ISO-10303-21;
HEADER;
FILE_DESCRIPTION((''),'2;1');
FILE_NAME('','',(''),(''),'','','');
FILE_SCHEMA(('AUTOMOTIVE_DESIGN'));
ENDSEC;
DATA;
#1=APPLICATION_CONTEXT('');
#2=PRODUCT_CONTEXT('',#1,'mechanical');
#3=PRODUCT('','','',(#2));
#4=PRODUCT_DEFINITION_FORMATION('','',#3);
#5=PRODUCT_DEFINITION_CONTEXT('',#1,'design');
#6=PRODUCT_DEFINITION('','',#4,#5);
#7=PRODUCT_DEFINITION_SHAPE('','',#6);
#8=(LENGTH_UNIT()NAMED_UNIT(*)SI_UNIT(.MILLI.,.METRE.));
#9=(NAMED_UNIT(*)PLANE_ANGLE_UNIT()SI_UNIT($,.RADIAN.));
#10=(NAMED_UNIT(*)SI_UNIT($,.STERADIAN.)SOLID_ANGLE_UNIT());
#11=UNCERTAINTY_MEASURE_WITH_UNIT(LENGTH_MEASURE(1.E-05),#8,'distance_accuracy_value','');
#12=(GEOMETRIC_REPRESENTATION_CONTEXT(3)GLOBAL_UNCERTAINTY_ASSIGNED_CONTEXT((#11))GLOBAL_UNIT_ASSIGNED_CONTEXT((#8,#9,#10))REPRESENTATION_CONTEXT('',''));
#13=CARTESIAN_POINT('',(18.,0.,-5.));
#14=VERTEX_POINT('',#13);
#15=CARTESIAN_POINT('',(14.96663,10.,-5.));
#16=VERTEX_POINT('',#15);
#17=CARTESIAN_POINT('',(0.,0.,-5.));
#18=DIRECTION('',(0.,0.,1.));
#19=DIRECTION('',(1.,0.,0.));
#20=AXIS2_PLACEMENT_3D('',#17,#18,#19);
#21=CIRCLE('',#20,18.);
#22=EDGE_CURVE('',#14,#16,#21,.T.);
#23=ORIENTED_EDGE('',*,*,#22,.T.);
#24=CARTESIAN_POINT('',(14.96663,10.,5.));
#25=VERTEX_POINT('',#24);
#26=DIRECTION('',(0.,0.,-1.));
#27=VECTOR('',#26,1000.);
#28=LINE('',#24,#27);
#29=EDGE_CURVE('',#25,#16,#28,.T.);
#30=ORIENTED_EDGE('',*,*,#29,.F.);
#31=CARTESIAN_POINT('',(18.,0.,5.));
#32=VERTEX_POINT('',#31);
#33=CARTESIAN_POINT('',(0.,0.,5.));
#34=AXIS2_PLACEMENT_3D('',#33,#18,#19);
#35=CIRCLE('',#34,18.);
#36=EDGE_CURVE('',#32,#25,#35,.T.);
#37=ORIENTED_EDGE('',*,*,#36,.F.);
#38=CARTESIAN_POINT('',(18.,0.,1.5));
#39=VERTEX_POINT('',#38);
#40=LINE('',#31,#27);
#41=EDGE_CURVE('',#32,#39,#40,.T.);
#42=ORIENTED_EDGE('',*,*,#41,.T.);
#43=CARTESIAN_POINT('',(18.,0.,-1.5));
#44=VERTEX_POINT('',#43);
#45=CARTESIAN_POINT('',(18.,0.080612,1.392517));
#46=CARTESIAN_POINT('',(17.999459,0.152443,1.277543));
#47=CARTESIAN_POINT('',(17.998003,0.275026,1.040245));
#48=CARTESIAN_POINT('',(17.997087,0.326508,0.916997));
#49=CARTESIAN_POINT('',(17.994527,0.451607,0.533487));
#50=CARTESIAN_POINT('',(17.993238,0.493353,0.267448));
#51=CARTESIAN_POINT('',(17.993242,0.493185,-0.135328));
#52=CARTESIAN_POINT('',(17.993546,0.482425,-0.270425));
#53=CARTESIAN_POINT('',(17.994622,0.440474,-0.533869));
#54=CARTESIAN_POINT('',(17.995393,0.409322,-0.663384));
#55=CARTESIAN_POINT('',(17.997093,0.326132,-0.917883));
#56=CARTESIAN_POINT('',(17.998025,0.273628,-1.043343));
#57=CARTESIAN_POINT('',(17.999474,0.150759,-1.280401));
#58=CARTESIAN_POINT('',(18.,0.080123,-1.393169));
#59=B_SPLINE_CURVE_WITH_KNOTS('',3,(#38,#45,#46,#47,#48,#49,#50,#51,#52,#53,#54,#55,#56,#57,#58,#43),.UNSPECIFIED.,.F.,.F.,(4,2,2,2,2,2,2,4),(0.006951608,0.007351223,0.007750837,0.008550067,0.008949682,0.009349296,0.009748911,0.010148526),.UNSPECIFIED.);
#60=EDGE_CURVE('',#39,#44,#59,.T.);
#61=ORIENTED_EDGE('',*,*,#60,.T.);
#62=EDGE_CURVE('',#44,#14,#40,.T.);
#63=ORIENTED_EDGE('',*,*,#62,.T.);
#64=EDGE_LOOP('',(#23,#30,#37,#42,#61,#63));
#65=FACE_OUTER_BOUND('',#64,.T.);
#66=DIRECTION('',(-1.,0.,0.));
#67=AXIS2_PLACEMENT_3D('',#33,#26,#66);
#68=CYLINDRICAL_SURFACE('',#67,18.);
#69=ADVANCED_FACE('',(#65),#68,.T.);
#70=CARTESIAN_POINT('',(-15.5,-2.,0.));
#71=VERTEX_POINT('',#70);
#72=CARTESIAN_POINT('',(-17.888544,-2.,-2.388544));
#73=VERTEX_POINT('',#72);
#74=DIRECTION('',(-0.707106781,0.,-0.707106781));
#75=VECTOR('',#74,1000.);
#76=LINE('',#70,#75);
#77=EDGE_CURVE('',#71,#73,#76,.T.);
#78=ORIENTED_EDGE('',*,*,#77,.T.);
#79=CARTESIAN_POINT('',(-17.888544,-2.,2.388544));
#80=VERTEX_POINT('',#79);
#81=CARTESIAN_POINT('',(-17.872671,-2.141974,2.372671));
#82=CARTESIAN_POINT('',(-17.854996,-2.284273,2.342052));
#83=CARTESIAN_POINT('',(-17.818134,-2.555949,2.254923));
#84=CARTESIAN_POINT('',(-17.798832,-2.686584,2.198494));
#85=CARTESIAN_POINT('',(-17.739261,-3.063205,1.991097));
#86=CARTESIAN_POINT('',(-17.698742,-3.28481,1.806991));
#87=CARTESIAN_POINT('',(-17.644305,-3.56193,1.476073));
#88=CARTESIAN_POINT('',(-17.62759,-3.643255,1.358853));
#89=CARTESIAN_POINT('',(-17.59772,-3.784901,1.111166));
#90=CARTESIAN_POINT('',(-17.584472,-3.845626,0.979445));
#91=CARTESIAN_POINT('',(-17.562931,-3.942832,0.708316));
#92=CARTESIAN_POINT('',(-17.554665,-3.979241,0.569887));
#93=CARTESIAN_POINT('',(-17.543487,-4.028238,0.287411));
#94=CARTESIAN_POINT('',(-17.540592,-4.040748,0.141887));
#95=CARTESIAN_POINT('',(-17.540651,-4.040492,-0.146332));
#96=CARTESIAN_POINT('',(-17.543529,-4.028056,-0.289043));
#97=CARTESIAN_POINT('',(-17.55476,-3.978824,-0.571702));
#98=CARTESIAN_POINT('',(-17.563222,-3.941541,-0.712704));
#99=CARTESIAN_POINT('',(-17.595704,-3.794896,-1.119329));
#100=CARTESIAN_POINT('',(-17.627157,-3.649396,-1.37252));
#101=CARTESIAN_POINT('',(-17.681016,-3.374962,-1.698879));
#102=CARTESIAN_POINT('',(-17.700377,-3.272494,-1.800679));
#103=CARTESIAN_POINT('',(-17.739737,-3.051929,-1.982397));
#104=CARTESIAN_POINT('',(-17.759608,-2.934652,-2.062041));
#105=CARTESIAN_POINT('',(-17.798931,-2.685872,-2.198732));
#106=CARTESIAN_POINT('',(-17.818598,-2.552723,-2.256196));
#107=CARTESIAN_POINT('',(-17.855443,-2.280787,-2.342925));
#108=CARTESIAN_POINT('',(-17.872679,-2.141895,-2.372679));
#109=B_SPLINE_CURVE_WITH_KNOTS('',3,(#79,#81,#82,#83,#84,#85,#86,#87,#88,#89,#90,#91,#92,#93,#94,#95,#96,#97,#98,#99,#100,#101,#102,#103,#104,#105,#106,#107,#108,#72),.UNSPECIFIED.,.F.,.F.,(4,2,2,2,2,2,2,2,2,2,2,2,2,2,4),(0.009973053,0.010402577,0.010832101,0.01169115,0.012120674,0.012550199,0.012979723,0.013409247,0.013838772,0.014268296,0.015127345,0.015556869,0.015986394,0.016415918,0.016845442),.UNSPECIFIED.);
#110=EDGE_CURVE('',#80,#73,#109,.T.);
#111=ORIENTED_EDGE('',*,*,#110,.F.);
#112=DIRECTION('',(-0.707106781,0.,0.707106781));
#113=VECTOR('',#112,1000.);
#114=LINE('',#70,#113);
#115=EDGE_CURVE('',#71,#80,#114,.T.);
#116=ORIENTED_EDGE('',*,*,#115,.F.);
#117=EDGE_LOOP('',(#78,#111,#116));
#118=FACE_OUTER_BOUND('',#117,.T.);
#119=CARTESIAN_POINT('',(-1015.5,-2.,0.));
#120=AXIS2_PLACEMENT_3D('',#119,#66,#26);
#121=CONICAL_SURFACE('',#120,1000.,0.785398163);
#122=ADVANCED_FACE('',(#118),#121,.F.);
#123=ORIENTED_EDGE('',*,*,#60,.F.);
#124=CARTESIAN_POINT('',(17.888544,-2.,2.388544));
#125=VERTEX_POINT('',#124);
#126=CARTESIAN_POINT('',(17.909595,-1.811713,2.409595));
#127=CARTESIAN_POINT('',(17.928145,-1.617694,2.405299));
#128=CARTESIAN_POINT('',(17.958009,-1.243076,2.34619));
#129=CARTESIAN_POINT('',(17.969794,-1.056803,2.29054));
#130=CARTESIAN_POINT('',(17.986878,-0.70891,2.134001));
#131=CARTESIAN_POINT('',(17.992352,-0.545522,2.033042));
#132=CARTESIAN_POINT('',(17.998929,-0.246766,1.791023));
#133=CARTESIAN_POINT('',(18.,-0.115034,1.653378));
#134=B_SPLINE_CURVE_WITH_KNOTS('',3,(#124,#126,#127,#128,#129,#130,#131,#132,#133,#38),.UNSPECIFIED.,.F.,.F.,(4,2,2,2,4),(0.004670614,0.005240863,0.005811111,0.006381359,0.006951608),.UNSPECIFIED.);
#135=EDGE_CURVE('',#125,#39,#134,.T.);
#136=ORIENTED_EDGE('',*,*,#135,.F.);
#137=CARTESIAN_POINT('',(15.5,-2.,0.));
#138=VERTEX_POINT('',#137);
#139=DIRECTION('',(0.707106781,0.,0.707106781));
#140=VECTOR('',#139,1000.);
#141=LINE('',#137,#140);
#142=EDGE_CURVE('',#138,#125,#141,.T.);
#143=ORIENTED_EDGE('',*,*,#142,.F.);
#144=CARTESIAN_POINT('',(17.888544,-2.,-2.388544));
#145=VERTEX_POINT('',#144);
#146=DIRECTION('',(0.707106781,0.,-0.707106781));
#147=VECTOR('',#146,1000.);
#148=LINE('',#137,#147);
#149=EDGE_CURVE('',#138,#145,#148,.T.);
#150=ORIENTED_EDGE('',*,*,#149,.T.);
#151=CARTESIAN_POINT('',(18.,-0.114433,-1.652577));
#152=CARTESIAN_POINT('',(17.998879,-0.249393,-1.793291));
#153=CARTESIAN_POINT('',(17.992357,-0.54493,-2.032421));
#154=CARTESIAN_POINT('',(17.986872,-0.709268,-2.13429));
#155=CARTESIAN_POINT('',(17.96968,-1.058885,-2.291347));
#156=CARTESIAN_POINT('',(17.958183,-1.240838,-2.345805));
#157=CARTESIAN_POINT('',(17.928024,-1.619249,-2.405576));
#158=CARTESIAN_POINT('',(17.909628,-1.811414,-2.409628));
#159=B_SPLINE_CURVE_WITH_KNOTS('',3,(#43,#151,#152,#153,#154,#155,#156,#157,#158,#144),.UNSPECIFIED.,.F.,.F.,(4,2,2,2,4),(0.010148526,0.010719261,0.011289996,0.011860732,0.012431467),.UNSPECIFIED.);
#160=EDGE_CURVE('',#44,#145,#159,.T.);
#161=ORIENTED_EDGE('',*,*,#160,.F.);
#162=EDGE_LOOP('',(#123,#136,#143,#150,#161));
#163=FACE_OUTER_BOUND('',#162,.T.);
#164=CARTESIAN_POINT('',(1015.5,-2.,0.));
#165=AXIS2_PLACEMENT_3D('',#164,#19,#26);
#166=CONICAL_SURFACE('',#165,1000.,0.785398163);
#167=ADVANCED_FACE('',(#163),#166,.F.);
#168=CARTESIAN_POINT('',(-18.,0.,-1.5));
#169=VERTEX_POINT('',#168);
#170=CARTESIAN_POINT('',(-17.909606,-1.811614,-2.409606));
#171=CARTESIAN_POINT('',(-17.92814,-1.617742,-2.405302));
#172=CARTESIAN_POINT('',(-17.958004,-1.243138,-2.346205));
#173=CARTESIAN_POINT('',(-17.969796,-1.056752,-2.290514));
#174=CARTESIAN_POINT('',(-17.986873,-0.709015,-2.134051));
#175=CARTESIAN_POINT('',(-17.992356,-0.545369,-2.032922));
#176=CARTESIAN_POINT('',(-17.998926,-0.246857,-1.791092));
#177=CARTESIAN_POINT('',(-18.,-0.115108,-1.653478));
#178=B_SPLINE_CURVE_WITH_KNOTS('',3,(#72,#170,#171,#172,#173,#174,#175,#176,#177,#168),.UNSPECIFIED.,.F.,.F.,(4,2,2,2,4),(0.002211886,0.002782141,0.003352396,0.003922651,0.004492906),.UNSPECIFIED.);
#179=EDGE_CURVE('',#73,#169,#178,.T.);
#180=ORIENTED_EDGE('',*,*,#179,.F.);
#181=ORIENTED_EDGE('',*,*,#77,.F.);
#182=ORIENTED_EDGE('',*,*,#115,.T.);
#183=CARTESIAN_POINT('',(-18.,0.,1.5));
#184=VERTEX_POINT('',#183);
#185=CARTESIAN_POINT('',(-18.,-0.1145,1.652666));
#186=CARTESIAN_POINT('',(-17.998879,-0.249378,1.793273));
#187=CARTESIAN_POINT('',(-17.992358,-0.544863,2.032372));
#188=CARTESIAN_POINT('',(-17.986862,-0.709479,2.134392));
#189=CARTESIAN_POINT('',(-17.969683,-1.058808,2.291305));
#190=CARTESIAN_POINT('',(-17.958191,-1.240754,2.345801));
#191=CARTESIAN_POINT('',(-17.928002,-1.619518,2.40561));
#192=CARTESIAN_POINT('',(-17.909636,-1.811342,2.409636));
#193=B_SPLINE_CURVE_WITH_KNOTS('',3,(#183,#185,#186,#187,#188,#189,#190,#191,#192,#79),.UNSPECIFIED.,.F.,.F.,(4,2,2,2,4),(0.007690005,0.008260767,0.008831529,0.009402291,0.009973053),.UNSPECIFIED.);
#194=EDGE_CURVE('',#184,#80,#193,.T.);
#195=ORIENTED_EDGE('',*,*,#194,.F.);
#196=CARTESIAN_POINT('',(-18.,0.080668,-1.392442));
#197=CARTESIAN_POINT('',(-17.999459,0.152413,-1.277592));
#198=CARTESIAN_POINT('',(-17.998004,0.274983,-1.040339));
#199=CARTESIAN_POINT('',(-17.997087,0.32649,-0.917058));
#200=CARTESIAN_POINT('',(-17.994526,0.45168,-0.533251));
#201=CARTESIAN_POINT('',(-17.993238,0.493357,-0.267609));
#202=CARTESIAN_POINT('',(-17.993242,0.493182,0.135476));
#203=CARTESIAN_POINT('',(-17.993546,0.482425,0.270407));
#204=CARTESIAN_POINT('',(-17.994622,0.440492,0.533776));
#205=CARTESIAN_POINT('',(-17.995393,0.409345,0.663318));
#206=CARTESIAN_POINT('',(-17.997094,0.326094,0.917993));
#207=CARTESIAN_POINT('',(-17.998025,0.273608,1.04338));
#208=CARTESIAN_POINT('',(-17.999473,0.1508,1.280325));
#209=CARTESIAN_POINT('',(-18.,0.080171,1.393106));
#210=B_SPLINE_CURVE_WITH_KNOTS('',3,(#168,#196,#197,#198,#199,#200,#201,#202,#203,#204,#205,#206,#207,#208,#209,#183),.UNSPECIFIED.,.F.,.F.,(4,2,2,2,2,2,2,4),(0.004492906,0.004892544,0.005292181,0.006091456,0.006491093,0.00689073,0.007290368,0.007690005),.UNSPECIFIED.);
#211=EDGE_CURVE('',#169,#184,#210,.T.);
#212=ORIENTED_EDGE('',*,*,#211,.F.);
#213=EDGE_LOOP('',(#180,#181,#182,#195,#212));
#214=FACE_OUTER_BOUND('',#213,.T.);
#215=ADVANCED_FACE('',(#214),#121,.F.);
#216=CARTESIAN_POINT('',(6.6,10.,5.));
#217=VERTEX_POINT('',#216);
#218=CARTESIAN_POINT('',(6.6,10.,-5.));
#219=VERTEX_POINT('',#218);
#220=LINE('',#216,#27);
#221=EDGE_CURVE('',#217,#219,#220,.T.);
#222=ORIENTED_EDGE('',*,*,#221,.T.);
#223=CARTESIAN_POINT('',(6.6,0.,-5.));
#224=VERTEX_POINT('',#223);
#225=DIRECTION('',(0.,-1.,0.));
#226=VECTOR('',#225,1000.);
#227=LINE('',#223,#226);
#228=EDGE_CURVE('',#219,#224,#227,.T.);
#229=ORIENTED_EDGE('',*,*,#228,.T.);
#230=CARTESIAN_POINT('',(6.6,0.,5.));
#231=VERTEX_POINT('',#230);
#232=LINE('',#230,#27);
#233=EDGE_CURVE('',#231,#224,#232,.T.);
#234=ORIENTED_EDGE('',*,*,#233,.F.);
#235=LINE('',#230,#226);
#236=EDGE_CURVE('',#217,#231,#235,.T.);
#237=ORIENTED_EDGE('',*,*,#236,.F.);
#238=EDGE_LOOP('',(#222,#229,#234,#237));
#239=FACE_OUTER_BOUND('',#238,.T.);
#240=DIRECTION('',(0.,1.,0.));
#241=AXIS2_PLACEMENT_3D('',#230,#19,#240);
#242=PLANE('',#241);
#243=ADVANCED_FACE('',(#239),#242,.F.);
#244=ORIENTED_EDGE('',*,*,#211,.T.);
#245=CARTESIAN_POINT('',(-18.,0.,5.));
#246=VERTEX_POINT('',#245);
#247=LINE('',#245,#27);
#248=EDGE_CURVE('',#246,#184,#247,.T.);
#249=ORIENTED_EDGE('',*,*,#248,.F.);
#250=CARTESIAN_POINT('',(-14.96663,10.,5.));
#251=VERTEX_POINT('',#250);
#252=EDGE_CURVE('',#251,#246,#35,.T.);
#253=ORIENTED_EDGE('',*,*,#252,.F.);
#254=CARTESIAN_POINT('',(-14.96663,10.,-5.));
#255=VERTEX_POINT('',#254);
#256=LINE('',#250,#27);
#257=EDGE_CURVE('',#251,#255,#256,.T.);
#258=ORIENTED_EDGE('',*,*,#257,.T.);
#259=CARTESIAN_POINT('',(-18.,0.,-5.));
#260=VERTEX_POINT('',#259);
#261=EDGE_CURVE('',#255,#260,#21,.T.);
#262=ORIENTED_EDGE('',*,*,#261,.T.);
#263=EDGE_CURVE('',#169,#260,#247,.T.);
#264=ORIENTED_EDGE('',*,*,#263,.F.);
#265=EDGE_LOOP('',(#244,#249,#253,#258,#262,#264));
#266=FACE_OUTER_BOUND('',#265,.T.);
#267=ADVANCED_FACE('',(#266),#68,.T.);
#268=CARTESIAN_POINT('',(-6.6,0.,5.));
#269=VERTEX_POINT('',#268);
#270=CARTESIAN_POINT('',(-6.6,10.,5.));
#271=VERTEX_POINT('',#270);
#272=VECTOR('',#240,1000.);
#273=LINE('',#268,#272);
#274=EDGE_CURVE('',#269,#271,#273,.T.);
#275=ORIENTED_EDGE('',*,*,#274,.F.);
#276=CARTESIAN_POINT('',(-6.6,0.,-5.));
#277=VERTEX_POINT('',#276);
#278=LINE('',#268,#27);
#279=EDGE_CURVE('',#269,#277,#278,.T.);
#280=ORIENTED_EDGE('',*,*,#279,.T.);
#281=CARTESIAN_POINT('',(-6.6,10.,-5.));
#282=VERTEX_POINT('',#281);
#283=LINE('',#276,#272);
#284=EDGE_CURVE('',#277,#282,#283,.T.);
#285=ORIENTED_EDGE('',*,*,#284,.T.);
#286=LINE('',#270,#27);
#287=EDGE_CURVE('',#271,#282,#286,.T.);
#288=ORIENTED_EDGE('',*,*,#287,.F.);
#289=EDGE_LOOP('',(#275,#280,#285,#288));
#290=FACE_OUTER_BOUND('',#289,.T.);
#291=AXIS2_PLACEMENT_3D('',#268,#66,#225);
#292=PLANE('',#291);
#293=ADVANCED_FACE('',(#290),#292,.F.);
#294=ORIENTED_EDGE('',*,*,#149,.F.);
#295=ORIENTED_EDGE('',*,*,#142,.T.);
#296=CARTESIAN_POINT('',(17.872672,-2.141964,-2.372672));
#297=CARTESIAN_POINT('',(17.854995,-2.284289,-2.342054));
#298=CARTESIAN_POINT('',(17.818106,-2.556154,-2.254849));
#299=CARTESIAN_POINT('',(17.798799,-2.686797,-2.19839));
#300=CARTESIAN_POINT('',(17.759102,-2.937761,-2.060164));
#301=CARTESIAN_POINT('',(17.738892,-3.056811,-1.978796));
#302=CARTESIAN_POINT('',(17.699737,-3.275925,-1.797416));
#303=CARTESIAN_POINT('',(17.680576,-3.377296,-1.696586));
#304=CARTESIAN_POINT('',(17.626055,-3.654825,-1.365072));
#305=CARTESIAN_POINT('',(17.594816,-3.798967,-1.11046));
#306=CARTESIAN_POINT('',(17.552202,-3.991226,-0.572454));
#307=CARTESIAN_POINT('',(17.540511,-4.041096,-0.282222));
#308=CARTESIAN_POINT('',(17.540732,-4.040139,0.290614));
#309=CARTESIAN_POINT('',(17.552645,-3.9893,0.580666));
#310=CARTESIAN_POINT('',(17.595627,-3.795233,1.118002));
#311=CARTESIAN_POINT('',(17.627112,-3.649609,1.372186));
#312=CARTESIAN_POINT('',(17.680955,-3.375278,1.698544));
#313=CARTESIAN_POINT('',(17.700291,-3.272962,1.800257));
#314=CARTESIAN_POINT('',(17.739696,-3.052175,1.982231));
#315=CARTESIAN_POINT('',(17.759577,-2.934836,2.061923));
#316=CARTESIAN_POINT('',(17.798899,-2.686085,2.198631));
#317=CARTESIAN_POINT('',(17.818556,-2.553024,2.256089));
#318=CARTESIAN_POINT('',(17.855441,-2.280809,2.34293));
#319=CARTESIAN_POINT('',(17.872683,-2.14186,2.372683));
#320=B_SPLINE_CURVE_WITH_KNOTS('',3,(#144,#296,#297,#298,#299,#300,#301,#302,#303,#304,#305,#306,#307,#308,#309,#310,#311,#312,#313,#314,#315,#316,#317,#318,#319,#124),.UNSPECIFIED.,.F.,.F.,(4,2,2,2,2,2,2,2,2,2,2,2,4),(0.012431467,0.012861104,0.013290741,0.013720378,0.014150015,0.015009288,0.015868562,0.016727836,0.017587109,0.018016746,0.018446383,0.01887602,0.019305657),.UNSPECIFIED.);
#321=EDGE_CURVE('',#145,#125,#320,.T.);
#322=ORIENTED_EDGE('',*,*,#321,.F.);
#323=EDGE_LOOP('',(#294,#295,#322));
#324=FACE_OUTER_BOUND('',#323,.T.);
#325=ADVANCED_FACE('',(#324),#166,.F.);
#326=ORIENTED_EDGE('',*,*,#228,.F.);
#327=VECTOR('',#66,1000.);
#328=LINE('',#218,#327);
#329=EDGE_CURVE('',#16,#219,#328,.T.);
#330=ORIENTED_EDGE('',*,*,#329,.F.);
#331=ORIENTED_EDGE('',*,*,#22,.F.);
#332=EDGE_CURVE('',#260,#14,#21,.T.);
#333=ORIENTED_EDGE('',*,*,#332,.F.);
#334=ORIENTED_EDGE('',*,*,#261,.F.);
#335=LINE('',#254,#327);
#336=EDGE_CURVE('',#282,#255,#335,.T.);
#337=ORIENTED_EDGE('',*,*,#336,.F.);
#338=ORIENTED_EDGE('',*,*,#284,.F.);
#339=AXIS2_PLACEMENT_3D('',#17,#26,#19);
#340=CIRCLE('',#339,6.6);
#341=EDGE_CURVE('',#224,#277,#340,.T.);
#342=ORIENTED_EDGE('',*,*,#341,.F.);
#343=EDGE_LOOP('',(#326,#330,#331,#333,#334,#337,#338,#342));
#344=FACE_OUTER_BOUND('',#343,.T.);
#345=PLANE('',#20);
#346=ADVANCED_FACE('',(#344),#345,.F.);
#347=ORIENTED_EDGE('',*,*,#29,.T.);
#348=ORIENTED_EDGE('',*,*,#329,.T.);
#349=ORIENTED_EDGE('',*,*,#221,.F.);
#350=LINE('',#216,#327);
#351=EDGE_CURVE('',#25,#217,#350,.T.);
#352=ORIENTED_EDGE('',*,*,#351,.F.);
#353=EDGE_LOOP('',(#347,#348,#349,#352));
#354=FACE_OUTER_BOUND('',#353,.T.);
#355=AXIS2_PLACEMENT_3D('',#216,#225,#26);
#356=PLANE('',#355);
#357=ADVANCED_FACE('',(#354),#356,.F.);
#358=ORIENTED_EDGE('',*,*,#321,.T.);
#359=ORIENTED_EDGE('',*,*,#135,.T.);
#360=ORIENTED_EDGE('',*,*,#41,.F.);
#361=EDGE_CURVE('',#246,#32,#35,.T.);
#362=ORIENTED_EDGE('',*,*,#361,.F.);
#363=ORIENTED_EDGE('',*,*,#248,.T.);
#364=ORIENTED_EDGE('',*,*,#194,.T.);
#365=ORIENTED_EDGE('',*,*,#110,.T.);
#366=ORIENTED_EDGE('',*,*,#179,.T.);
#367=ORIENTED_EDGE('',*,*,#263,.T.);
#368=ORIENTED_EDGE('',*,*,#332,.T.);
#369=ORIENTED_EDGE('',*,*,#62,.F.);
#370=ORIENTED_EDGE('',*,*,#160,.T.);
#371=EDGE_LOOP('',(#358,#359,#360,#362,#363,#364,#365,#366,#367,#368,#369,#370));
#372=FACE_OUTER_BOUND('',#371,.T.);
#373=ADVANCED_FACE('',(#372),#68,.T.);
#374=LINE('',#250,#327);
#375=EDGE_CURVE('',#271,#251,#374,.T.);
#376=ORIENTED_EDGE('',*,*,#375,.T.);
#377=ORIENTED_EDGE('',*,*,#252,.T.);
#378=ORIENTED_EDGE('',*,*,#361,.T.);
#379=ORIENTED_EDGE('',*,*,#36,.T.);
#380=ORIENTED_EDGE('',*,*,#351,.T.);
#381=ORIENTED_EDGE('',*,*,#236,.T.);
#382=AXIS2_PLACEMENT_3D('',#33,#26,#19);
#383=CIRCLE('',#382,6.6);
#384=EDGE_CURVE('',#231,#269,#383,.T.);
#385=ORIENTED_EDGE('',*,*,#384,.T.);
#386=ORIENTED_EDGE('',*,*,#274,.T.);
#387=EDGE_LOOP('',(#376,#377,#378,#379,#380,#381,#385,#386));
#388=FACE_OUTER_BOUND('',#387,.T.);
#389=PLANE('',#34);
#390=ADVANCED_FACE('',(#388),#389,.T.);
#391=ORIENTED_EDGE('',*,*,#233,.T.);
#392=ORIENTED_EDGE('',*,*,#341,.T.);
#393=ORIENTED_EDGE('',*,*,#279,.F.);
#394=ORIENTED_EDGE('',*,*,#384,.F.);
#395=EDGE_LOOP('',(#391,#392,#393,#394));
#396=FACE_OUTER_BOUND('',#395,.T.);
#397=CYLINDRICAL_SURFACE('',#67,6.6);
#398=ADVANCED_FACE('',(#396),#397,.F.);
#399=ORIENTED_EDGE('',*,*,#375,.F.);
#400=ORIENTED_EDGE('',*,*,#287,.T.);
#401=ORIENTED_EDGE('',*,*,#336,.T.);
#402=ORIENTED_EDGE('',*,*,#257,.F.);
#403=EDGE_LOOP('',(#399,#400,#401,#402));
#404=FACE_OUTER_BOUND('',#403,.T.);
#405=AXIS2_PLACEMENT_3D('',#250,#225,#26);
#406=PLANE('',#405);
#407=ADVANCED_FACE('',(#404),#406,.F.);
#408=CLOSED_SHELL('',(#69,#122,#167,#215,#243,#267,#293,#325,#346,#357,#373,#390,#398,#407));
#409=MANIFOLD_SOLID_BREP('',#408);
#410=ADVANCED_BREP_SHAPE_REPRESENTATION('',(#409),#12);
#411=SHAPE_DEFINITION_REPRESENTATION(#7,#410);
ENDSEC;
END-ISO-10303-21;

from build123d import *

# Parameters (mm, degrees)
BOSS_EXTRUDE1_DEPTH = 5


with BuildPart() as part:
    # Sketch1 → Boss-Extrude1 (new, symmetric)
    with BuildSketch(Plane.XY):
        with BuildLine():
            Line((-14.966629547, 10), (-6.6, 10))
            Line((-6.6, 10), (-6.6, 0))
            ThreePointArc((-6.6, 0), (0, -6.6), (6.6, 0))
            Line((6.6, 0), (6.6, 10))
            Line((6.6, 10), (14.966629547, 10))
            ThreePointArc((14.966629547, 10), (0, -18), (-14.966629547, 10))
        make_face()
    extrude(amount=BOSS_EXTRUDE1_DEPTH, both=True)

    # Sketch2 → Cut-Revolve1 (revolve, cut)
    with BuildSketch(Plane.XY, mode=Mode.PRIVATE) as cut_revolve1_sk:
        Polygon((18.861572054, -5.361572054), (18.861572054, -2), (15.5, -2), align=None)
    cut_revolve1 = revolve(cut_revolve1_sk.sketch.rotate(Axis((-24.047626866, -2, 0), (1, 0, 0)), 90), axis=Axis((-24.047626866, -2, 0), (1, 0, 0)), mode=Mode.SUBTRACT)

    # Mirror1: Cut-Revolve1 across plane
    add(cut_revolve1.mirror(Plane(origin=(0, 0, 0), x_dir=(0, 0, 1), z_dir=(1, 0, 0))), mode=Mode.SUBTRACT)


solid = part.part
